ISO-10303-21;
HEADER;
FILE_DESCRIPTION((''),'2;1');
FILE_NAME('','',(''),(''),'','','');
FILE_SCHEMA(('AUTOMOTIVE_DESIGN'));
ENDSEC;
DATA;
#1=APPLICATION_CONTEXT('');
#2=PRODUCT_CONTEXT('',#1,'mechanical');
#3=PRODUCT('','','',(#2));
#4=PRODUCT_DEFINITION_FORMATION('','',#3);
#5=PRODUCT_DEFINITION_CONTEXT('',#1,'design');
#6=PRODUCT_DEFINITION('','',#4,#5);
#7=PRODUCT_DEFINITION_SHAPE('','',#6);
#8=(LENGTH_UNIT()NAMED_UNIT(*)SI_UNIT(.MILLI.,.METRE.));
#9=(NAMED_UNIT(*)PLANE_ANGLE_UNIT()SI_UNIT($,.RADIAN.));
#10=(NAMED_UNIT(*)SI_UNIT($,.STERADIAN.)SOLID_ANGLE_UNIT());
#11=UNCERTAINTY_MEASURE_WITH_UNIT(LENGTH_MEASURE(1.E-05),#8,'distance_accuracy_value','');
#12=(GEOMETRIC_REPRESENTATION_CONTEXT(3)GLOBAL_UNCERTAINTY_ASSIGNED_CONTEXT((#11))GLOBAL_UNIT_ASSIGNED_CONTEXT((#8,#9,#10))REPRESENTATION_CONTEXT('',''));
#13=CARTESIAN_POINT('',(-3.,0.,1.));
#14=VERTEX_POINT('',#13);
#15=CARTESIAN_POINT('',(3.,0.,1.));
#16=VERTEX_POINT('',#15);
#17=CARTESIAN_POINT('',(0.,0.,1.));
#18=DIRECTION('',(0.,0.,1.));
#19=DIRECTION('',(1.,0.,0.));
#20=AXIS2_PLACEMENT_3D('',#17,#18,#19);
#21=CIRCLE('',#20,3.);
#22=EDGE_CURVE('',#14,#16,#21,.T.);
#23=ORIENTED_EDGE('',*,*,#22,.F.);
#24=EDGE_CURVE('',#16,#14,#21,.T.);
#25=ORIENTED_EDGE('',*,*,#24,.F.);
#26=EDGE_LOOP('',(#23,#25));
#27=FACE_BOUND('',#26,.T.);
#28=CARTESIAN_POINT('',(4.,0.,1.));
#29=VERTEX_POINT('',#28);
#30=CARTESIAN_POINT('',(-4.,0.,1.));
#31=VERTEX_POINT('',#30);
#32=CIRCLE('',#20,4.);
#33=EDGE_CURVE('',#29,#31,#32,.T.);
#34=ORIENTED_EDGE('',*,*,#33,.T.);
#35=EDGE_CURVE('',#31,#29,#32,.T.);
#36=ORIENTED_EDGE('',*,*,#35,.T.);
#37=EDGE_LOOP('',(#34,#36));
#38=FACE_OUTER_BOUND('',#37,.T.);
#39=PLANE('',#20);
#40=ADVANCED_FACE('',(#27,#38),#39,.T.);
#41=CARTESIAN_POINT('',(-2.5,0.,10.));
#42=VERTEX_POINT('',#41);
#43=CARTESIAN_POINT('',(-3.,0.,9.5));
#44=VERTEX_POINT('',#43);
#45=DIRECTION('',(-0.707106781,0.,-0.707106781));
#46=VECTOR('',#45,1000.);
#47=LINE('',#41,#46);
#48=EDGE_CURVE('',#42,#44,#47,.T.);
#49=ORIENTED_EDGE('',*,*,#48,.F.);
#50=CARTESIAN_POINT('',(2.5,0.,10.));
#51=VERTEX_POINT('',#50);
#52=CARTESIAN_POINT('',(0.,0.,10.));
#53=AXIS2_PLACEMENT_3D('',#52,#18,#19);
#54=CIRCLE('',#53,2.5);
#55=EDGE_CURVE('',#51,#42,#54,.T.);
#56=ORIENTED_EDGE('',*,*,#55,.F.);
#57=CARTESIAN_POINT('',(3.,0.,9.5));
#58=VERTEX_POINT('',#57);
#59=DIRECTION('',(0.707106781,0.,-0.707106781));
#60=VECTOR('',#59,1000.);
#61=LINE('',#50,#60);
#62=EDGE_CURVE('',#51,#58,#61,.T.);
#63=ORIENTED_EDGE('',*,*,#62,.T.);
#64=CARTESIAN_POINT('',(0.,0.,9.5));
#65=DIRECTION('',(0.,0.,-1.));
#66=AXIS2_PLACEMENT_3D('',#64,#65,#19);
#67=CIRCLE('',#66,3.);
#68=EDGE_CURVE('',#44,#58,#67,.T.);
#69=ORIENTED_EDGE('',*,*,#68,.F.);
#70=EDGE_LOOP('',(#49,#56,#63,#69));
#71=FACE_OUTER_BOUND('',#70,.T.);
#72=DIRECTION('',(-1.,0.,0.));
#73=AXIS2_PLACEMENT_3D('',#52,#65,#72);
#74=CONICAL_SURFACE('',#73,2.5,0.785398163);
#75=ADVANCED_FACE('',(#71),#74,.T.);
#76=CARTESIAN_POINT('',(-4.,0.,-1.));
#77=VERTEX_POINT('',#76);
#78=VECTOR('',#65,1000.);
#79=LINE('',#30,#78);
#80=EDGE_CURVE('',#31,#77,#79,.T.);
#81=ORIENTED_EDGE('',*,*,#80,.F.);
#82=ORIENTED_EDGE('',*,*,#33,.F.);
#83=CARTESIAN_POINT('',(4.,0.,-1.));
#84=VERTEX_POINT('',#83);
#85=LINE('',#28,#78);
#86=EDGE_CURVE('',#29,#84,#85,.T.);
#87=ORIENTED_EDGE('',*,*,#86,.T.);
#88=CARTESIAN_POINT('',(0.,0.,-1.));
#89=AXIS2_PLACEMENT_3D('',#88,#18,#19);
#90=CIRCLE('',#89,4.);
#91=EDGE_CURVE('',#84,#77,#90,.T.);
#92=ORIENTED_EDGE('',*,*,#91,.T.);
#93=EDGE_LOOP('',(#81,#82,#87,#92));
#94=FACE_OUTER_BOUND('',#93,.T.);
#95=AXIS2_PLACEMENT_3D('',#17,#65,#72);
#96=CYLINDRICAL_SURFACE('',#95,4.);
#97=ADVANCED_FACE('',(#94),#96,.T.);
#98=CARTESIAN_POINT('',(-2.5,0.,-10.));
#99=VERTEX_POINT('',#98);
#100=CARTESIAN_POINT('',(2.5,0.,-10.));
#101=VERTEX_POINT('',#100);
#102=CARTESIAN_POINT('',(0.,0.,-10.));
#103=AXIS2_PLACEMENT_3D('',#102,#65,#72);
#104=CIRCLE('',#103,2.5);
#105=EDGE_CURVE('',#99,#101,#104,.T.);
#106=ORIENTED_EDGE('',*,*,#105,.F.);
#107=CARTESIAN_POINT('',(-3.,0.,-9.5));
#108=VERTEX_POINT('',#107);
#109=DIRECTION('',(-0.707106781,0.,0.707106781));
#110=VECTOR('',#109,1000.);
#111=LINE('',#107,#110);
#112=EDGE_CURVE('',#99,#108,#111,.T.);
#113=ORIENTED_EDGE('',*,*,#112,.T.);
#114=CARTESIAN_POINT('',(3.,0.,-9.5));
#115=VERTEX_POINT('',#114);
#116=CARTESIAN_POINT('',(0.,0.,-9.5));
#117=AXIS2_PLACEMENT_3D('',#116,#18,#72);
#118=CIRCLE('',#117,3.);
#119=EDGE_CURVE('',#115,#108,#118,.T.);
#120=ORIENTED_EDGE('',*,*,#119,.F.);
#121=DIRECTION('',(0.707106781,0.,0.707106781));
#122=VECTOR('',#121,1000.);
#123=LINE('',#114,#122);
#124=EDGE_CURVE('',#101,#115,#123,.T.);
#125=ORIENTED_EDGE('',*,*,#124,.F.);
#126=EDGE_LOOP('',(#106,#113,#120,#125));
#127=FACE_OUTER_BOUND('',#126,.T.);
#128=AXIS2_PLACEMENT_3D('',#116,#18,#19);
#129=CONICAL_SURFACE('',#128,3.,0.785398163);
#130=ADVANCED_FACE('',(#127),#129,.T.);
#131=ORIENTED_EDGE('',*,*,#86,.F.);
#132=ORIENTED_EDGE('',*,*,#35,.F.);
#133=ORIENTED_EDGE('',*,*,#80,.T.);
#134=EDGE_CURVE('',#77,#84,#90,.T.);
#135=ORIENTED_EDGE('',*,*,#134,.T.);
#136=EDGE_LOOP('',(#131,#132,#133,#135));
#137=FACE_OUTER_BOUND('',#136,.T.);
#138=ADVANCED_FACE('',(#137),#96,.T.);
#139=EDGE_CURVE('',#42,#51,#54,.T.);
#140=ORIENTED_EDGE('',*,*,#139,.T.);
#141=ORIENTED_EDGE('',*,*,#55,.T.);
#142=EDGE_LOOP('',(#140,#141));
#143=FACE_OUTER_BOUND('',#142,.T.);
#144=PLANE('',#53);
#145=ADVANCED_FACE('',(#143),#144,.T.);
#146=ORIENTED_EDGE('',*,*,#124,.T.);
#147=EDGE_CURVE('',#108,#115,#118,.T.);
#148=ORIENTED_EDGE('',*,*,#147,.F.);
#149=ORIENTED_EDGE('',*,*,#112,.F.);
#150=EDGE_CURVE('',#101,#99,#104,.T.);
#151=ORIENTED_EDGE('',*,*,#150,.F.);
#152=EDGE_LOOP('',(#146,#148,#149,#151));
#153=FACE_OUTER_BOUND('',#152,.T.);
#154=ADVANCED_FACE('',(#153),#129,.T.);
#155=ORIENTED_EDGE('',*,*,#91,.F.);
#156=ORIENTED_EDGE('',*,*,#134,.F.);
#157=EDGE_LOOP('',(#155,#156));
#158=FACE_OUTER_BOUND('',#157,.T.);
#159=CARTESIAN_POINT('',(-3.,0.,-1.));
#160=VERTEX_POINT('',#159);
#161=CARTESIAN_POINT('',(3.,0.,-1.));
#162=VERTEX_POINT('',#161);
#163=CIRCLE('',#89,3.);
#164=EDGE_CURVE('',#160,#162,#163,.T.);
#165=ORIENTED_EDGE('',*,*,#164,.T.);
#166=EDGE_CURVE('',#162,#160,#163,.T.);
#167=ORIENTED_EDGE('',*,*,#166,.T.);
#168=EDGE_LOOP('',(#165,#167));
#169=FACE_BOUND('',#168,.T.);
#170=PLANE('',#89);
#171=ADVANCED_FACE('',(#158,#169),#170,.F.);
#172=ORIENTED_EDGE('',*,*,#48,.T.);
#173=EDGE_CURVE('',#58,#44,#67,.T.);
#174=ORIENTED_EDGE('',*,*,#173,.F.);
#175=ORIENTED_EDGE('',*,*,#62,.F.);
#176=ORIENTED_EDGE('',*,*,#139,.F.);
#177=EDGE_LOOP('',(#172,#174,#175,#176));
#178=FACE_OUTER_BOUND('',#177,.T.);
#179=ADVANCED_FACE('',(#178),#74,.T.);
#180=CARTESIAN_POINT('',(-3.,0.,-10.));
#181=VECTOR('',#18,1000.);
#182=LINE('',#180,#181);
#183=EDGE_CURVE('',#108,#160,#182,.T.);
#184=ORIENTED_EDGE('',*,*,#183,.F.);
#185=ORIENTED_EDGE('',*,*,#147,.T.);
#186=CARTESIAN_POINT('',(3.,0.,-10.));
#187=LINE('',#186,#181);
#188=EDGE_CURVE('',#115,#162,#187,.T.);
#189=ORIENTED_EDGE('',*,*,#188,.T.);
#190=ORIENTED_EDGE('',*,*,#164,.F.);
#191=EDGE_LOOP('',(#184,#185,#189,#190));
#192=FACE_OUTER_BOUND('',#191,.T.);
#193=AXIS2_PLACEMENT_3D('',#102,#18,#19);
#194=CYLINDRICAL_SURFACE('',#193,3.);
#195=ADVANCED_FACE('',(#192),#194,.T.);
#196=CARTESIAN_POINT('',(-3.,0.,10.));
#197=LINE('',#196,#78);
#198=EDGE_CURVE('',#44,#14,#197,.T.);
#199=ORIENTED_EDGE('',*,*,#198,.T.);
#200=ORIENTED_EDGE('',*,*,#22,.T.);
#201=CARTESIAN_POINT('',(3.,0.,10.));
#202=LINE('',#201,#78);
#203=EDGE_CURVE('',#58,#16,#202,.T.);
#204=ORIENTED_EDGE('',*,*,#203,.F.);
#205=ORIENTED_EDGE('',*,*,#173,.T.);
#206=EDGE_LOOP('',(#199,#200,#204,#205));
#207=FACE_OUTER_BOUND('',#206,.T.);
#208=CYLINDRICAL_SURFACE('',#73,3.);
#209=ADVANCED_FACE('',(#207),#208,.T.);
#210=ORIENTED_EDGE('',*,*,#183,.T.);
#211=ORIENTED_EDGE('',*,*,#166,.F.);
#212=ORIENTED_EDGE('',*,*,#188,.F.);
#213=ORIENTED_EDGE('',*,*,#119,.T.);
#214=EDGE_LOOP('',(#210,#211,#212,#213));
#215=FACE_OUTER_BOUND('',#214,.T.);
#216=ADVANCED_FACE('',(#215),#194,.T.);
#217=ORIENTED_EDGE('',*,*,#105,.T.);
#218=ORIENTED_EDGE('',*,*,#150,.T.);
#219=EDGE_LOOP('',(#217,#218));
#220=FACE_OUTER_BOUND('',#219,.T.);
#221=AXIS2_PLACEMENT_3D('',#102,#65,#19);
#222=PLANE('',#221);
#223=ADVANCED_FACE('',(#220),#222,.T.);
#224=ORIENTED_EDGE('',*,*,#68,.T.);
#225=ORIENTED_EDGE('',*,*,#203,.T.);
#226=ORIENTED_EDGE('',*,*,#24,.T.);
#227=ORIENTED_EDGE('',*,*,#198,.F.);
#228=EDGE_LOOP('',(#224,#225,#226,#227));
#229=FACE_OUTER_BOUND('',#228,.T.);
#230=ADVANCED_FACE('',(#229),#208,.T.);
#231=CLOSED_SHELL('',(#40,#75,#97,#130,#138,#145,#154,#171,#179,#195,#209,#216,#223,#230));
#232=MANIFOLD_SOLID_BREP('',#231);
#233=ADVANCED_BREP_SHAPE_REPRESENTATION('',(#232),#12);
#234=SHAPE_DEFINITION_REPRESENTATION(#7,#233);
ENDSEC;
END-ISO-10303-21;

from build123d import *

# Parameters (mm, degrees)
SKETCH_1_R      = 4
EXTRUDE_1_DEPTH = 1
SKETCH_2_R      = 3
EXTRUDE_2_DEPTH = 9
CHAMFER_1_SIZE  = 0.5


with BuildPart() as part:
    # 草图1 → 凸台-拉伸1 (new, symmetric)
    with BuildSketch(Plane.XY):
        Circle(SKETCH_1_R)
    extrude(amount=EXTRUDE_1_DEPTH, both=True)

    # 草图2 → 凸台-拉伸2 (add)
    with BuildSketch(Plane.XY.offset(1)):
        Circle(SKETCH_2_R)
    extrude_2 = extrude(amount=EXTRUDE_2_DEPTH)

    # 镜向5: 凸台-拉伸2 across plane
    add(extrude_2.mirror(Plane.XY))

    # 倒角1
    chamfer_1_edges = [part.edges().sort_by_distance(p)[0] for p in [
        (-3, 0, -10),
        (-3, 0, 10),
    ]]
    chamfer(chamfer_1_edges, length=CHAMFER_1_SIZE)


solid = part.part
